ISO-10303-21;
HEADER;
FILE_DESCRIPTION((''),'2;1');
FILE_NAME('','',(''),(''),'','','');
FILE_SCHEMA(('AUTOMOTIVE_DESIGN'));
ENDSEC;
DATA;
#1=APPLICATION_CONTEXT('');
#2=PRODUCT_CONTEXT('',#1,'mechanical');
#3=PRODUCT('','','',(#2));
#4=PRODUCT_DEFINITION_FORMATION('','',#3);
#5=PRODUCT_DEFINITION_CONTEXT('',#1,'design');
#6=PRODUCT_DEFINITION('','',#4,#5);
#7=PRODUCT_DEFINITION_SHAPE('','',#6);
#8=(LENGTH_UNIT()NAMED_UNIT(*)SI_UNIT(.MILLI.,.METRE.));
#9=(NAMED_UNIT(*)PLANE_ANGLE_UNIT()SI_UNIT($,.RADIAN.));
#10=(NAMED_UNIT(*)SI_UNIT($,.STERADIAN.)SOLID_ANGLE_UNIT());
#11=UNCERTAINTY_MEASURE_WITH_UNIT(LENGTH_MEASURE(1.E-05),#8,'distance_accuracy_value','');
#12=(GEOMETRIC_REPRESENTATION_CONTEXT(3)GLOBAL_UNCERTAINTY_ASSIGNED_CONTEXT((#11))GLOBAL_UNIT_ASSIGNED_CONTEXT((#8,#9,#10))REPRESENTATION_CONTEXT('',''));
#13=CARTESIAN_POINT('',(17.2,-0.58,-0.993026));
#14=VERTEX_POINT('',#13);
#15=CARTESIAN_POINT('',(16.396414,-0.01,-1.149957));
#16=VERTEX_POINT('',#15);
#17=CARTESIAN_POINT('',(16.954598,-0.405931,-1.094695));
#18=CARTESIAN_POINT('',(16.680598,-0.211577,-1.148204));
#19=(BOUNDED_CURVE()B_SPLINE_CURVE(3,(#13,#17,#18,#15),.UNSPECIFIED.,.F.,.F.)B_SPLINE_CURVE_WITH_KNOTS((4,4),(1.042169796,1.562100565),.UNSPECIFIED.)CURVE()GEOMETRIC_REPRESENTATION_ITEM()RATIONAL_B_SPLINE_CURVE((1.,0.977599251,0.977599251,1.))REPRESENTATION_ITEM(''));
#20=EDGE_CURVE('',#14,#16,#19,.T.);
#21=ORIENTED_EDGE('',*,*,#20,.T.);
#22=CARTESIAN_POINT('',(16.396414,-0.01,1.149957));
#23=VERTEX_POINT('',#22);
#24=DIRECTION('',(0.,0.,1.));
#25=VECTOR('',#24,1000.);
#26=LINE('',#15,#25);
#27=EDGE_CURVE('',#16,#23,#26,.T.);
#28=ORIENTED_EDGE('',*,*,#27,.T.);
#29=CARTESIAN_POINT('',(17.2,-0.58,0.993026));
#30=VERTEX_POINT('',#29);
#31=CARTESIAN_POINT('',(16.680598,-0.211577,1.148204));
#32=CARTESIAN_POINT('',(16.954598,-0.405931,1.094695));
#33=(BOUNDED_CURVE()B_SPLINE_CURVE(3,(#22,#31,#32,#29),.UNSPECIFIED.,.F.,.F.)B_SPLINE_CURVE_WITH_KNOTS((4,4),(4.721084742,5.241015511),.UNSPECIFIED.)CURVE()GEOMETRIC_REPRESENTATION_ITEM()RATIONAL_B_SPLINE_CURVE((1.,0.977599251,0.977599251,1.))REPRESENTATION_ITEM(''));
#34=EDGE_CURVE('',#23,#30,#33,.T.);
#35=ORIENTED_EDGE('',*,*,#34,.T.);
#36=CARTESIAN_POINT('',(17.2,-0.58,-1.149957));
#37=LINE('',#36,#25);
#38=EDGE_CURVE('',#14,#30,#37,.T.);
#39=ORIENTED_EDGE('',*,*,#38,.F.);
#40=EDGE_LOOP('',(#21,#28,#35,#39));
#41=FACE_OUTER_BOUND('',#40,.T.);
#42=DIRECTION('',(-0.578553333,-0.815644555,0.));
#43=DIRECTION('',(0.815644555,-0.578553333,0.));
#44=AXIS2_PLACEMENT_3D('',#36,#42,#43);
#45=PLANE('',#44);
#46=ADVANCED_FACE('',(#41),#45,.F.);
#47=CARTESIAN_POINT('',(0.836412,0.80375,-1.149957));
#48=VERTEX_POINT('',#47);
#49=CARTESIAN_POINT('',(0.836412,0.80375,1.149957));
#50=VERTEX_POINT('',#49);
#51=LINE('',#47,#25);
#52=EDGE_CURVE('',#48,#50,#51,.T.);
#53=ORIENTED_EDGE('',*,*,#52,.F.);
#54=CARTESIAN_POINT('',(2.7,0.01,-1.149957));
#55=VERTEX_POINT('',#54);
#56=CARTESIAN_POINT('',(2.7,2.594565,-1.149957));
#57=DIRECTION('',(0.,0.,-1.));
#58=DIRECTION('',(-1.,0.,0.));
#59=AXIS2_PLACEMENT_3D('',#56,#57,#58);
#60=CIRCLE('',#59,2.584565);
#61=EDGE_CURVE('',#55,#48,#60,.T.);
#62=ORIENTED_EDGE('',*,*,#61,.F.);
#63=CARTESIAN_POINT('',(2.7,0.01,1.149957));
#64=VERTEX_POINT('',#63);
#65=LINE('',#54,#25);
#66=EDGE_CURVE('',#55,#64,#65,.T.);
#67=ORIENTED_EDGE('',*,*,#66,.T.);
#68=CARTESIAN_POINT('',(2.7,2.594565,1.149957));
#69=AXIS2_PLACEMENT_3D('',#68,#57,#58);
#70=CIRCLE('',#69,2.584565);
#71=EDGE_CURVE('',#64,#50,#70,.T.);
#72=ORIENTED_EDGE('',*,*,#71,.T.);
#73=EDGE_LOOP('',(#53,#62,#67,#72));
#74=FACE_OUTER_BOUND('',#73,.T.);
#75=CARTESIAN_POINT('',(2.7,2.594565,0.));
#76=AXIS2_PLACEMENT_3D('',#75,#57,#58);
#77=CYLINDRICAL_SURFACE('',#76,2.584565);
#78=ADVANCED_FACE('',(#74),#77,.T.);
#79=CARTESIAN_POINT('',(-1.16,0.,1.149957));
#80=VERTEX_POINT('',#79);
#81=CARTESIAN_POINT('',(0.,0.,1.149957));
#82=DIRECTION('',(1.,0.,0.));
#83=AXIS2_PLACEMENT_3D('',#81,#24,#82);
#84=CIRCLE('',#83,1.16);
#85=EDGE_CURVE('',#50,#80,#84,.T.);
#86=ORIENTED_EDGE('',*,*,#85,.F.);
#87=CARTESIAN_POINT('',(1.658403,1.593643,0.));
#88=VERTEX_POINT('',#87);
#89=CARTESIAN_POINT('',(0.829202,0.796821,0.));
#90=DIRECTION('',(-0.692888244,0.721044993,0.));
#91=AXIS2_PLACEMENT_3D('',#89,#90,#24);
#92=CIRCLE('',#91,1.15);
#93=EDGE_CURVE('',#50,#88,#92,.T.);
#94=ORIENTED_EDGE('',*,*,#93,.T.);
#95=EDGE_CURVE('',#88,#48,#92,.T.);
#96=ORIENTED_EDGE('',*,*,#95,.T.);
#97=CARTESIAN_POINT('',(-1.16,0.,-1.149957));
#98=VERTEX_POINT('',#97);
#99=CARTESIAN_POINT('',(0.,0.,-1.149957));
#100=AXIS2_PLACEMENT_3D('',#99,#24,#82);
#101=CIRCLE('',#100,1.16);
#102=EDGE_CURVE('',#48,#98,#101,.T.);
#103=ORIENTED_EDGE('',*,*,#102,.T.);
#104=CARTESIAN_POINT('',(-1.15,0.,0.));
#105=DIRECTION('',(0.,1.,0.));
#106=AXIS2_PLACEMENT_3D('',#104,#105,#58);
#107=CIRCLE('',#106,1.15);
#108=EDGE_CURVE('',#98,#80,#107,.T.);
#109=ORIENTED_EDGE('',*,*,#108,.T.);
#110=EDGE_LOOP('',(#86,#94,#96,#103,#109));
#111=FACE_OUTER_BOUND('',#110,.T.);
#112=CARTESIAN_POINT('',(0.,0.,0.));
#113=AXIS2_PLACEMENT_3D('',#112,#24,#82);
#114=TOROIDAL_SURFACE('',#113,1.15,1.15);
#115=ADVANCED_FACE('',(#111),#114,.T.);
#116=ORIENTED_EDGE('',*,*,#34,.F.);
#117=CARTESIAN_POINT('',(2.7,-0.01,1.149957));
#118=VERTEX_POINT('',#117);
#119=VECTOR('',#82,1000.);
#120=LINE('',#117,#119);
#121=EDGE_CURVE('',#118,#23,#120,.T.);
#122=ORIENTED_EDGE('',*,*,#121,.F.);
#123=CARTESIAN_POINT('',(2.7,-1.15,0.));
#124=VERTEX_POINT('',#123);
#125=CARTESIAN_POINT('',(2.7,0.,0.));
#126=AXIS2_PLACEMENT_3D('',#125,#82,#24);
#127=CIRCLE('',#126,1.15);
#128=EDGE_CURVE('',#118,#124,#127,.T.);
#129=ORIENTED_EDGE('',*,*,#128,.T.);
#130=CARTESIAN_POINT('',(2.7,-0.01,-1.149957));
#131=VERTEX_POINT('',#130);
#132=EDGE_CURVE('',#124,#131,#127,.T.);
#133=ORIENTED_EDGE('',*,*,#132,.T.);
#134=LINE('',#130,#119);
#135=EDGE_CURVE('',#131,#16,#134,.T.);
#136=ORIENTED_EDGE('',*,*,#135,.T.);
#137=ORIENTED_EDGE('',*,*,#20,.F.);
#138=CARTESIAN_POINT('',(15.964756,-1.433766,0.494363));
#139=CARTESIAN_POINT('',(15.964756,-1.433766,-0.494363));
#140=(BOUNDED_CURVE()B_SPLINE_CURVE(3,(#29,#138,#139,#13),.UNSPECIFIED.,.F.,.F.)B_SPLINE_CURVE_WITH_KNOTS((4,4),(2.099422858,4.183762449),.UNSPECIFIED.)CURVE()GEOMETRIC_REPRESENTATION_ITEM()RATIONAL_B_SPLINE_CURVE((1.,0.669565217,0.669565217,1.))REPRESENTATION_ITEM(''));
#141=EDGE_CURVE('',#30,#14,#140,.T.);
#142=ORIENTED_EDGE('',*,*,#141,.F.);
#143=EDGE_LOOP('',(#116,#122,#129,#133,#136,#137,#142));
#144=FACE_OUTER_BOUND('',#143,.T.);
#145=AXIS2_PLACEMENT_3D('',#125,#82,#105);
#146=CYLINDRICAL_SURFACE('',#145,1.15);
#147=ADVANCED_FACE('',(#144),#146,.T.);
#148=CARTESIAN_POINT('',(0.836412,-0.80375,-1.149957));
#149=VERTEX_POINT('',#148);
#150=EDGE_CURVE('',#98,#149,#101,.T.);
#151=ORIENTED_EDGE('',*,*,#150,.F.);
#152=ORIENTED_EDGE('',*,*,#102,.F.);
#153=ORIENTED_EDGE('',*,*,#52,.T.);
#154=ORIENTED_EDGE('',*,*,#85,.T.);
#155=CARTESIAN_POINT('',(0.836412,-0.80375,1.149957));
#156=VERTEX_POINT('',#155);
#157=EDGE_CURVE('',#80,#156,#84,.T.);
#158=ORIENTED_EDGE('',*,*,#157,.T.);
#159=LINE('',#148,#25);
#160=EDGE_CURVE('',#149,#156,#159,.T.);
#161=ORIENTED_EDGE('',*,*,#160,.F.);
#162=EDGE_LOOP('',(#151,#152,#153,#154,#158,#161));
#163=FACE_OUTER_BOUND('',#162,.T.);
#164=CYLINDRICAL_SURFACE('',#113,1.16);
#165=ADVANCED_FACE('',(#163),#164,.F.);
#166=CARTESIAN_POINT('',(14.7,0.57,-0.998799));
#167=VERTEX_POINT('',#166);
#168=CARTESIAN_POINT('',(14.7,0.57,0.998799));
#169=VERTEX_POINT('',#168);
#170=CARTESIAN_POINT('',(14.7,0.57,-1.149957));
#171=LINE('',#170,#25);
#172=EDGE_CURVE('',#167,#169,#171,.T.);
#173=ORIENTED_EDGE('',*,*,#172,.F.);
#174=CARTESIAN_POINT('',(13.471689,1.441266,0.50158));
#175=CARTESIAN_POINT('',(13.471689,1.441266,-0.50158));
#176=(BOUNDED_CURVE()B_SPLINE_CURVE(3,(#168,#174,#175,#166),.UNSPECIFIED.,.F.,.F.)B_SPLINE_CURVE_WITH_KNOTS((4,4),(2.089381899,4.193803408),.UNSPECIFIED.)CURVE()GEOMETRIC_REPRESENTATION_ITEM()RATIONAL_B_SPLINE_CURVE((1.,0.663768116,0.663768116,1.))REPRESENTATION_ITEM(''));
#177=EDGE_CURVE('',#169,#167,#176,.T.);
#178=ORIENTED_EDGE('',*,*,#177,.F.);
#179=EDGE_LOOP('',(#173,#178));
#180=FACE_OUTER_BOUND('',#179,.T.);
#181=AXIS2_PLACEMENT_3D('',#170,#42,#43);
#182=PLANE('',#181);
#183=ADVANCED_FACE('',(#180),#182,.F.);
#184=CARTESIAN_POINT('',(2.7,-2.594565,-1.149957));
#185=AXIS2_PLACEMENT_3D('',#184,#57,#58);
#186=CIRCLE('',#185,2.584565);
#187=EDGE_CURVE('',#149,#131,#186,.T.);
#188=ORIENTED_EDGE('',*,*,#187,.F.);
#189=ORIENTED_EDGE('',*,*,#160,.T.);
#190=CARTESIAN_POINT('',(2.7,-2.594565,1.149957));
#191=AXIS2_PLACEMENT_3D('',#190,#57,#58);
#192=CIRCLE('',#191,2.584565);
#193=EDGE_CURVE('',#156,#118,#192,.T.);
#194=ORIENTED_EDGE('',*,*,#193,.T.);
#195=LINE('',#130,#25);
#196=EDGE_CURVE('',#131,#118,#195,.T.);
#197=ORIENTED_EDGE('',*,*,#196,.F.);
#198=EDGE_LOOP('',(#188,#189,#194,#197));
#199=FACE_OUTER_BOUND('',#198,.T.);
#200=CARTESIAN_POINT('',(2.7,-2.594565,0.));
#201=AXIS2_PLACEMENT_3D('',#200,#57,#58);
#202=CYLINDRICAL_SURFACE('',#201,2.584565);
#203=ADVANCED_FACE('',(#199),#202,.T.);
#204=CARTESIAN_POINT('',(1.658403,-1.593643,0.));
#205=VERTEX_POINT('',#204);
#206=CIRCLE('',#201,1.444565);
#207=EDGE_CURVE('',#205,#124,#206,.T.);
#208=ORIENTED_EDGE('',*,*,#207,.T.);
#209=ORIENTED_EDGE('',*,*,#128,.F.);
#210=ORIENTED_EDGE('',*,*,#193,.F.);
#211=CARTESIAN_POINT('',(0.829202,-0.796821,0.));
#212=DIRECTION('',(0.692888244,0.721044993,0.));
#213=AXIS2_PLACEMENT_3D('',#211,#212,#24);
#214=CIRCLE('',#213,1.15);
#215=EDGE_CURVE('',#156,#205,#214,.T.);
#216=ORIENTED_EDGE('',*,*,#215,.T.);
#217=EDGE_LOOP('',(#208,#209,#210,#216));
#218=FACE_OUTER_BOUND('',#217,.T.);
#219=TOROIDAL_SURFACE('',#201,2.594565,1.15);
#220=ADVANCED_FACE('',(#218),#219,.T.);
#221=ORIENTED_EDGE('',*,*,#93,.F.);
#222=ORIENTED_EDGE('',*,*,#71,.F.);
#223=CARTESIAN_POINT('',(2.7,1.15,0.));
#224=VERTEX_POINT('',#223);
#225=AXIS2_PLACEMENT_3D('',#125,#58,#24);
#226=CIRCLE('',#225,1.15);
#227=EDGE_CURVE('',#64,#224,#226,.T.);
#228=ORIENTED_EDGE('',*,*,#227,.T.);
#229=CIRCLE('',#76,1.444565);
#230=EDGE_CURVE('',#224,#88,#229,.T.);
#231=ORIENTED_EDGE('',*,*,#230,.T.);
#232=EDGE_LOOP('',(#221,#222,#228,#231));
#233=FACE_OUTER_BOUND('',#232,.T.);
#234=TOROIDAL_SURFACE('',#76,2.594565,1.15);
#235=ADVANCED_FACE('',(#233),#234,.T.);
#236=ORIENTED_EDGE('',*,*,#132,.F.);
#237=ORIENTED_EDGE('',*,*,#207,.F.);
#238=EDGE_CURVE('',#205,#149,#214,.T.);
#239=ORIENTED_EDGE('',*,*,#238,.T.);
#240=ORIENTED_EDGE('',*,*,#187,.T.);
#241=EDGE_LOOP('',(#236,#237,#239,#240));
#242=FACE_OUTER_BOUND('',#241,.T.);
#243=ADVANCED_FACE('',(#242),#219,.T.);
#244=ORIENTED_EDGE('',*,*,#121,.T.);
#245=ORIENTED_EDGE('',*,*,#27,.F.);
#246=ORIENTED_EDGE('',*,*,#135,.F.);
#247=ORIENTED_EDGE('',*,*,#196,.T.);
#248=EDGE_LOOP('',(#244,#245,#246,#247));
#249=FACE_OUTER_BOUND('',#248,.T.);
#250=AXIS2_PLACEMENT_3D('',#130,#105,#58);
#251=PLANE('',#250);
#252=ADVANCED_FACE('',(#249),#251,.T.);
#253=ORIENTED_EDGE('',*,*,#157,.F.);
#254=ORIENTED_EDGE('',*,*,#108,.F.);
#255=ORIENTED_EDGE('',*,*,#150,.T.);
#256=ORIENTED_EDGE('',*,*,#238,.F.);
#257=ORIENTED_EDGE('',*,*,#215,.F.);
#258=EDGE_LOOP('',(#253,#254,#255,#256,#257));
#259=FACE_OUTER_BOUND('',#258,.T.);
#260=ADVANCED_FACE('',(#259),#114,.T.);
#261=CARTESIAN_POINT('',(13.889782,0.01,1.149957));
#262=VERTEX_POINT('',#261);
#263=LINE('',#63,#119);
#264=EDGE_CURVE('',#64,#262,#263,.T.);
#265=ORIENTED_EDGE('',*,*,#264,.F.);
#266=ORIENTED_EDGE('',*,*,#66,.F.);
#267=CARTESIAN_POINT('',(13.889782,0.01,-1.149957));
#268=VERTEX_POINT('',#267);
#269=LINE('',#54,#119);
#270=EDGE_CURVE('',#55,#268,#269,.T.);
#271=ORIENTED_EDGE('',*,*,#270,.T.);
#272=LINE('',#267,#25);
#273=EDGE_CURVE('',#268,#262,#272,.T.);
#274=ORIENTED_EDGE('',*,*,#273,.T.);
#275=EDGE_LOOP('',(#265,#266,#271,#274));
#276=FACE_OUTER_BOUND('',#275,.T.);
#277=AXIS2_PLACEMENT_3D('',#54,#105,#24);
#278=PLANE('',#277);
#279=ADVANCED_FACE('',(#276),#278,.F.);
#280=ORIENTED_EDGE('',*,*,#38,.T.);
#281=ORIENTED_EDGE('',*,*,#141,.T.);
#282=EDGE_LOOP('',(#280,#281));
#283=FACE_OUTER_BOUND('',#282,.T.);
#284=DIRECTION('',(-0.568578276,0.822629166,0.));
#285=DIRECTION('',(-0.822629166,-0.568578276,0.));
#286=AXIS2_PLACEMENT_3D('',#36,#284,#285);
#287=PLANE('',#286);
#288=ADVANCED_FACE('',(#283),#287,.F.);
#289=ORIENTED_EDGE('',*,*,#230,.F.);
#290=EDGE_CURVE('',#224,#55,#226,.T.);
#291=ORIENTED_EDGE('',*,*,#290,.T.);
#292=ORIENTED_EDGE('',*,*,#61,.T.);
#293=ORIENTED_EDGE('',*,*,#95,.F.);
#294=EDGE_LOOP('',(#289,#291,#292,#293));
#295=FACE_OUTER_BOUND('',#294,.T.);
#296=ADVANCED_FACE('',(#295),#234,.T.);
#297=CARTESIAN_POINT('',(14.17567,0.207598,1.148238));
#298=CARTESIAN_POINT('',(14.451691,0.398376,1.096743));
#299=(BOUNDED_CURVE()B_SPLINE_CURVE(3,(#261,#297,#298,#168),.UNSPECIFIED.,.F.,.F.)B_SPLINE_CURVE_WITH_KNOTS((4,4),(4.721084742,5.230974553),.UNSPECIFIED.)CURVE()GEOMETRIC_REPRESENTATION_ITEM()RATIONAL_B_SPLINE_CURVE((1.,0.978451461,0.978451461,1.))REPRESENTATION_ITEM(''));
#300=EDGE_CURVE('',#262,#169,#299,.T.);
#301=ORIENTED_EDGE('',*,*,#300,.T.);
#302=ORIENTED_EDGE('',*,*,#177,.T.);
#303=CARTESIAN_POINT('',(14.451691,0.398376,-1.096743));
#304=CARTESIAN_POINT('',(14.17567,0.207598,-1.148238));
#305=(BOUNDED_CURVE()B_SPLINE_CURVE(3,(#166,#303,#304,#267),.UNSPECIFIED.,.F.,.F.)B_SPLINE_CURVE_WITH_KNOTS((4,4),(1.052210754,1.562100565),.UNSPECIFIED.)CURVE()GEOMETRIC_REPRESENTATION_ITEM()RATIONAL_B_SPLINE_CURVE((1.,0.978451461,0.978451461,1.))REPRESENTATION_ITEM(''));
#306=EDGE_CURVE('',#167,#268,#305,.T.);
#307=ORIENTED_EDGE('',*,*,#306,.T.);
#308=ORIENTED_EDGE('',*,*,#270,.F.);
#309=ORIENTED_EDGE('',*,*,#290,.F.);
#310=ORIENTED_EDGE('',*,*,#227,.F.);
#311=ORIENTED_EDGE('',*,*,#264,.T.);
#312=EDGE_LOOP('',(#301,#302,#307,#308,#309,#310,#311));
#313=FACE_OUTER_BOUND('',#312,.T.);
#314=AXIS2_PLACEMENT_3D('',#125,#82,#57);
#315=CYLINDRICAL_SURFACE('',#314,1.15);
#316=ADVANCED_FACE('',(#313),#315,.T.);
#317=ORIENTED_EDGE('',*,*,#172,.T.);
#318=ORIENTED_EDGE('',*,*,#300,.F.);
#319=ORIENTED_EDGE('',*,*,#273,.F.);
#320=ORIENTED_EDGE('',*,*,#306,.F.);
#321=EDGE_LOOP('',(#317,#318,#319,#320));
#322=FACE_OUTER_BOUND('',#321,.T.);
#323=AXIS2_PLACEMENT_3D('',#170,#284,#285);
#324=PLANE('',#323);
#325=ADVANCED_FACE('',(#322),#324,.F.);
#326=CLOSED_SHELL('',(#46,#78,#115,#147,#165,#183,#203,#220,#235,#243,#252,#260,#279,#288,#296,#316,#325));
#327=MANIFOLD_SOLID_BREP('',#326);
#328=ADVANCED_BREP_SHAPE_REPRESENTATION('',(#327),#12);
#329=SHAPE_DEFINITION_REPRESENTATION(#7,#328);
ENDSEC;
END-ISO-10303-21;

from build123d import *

# Parameters (mm, degrees)
CUT_EXTRUDE1_DEPTH      = 18.391158693
CUT_EXTRUDE1_DEPTH_BACK = 18.391158693


with BuildPart() as part:
    # Sweep2: sweep along a path in Dimension Sketch
    with BuildLine(Plane.XY) as sweep2_path:
        Line((14.7, 1.15), (2.7, 1.15))
        ThreePointArc((2.7, 1.15), (2.133929691, 1.265530578), (1.658403483, 1.593642961))
        ThreePointArc((1.658403483, 1.593642961), (-2.3, 0), (1.658403483, -1.593642961))
        ThreePointArc((1.658403483, -1.593642961), (2.133929691, -1.265530578), (2.7, -1.15))
        Line((2.7, -1.15), (17.2, -1.15))
    # Sketch2 → Sweep2 (sweep)
    with BuildSketch(Plane(origin=(14.7, 1.15, 0), x_dir=(0, 0, 1), z_dir=(-1, 0, 0))):
        with BuildLine():
            Line((-1.149956521, -1.14), (1.149956521, -1.14))
            ThreePointArc((1.149956521, -1.14), (0, 0), (-1.149956521, -1.14))
        make_face()
    sweep(path=sweep2_path.line)

    # Sketch3 → Cut-Extrude1 (cut, two sides: drawn at the far end of the back side and taken through both)
    with BuildSketch(Plane.XY.offset(-CUT_EXTRUDE1_DEPTH_BACK)):
        Polygon((14.7, 0.57), (13.882315934, 1.15), (17.21, 1.15), (17.21, -1.15), (16.375313858, -1.15), (17.2, -0.58), (16.382315934, 0), (13.875313858, 0), align=None)
    extrude(amount=CUT_EXTRUDE1_DEPTH + CUT_EXTRUDE1_DEPTH_BACK, mode=Mode.SUBTRACT)


solid = part.part
